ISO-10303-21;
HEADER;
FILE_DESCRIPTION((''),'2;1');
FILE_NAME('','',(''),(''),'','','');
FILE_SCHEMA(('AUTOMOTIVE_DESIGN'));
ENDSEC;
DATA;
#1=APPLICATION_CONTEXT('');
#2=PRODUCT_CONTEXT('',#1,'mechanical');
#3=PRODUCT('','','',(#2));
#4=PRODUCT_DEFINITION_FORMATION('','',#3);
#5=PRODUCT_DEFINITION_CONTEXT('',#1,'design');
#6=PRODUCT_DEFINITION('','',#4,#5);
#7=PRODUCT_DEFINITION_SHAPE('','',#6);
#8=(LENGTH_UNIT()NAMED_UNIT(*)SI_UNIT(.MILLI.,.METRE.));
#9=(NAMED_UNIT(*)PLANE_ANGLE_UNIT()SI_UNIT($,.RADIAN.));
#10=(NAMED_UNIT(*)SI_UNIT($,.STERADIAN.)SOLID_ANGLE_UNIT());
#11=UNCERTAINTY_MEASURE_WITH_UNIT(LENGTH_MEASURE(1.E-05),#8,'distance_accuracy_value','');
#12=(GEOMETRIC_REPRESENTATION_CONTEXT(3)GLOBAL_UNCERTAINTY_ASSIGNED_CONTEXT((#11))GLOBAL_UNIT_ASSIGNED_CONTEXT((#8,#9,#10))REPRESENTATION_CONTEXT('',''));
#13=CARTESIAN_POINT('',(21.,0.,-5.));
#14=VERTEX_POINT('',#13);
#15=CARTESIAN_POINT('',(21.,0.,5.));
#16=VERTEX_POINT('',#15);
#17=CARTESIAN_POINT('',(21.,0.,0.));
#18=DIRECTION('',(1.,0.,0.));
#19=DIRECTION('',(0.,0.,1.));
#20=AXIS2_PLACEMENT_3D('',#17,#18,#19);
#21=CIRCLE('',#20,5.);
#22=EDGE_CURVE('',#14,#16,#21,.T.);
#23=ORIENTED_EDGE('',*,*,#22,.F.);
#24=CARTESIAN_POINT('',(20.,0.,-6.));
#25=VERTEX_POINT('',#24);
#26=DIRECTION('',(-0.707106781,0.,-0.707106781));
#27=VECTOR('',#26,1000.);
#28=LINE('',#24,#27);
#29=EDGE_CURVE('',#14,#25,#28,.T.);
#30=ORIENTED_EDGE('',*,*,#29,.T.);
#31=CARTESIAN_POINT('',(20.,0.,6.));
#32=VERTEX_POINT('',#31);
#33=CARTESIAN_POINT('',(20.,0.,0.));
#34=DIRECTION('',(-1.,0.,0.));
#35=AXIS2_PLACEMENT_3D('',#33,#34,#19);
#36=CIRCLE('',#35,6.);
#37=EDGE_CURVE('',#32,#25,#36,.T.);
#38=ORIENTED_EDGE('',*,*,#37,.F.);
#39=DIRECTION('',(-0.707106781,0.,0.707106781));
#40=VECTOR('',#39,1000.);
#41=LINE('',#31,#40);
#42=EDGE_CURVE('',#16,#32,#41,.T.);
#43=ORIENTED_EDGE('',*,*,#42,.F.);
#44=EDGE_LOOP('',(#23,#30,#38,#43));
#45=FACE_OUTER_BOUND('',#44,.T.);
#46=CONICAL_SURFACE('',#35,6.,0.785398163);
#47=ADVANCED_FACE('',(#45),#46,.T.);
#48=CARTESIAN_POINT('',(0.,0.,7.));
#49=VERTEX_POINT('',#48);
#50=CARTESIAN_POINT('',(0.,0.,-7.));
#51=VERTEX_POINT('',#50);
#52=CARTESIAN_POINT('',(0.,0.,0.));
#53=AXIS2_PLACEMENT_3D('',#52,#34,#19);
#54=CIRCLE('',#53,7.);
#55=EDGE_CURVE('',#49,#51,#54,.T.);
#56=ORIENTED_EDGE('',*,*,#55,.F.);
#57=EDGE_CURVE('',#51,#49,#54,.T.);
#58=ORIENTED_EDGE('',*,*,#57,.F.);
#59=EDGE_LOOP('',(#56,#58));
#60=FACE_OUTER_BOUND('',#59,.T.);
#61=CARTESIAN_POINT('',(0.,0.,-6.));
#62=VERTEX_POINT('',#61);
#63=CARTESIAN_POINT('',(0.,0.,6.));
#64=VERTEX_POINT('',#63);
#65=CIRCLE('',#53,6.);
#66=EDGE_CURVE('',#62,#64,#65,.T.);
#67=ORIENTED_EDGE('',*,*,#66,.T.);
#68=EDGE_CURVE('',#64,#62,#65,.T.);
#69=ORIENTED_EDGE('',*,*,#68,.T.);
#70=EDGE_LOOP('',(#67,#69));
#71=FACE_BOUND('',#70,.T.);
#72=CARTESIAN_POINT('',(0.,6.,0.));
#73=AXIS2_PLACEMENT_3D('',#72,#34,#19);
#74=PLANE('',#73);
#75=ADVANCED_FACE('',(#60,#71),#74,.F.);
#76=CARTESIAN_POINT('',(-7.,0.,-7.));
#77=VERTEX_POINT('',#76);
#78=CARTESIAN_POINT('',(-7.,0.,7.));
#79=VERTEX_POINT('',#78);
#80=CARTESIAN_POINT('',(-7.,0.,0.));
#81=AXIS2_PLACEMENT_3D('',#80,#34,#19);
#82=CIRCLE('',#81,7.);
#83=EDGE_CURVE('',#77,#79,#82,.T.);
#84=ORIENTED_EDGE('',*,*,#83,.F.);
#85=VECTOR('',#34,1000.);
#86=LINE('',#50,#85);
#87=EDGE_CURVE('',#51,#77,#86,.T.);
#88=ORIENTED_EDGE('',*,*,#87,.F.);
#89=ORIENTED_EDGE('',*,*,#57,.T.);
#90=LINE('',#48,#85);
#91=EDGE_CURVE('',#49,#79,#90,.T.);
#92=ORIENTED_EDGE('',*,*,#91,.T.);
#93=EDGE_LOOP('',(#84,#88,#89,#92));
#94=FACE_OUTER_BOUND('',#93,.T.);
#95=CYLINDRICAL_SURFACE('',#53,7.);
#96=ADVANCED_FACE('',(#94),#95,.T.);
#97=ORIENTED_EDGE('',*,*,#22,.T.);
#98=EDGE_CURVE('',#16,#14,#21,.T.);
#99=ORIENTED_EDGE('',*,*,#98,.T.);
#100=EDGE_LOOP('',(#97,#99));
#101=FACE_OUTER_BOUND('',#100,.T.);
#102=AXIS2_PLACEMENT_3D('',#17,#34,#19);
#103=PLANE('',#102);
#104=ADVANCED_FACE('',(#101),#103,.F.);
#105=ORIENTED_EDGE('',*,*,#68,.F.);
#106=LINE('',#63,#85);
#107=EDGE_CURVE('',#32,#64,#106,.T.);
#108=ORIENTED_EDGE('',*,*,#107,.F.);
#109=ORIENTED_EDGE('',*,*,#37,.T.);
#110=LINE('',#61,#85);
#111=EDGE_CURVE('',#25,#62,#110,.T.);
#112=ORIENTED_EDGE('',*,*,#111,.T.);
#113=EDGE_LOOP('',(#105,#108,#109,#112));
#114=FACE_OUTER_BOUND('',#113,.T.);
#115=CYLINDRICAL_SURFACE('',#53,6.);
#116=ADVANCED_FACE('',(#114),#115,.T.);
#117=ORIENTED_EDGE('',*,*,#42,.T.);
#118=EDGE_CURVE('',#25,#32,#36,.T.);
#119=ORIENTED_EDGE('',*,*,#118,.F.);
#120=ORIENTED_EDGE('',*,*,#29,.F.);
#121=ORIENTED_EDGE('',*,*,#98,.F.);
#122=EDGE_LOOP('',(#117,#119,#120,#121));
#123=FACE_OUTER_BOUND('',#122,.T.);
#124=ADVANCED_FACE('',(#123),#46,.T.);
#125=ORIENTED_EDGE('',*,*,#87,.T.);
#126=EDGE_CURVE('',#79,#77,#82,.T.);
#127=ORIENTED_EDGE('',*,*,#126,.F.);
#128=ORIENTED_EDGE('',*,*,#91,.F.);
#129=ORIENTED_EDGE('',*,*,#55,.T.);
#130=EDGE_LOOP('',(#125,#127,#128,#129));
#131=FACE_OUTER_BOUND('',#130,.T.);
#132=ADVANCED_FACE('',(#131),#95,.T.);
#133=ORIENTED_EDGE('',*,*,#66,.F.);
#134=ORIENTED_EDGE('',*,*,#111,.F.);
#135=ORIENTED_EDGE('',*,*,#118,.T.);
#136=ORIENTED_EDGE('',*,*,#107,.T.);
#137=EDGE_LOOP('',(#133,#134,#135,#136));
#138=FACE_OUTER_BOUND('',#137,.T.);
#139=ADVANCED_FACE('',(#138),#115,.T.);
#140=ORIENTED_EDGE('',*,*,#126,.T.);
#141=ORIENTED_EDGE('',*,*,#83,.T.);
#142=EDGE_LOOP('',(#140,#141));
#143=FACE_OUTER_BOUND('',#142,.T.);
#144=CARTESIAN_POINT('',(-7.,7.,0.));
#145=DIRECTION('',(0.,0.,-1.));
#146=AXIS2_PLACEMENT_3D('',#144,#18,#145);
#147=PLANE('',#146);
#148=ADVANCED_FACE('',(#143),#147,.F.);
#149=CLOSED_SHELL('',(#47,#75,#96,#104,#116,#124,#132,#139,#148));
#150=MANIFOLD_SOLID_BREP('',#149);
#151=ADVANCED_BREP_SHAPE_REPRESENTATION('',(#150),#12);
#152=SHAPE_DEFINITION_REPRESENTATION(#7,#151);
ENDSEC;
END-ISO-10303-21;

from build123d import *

# Parameters (mm, degrees)
SHANK_TIP_CHAMFER_1X45_SIZE = 1


with BuildPart() as part:
    # Bolt Profile Sketch → Bolt Body Revolve (revolve)
    with BuildSketch(Plane.XY, mode=Mode.PRIVATE) as bolt_body_revolve_sk:
        Polygon((0, 0), (21, 0), (21, 6), (0, 6), (0, 7), (-7, 7), (-7, 0), align=None)
    revolve(bolt_body_revolve_sk.sketch.rotate(Axis((0, 0, 0), (1, 0, 0)), 90), axis=Axis((0, 0, 0), (1, 0, 0)))

    # Shank Tip Chamfer 1x45°
    shank_tip_chamfer_1x45_edges = [part.edges().sort_by_distance(p)[0] for p in [
        (21, 0, -6),
    ]]
    chamfer(shank_tip_chamfer_1x45_edges, length=SHANK_TIP_CHAMFER_1X45_SIZE)


solid = part.part
